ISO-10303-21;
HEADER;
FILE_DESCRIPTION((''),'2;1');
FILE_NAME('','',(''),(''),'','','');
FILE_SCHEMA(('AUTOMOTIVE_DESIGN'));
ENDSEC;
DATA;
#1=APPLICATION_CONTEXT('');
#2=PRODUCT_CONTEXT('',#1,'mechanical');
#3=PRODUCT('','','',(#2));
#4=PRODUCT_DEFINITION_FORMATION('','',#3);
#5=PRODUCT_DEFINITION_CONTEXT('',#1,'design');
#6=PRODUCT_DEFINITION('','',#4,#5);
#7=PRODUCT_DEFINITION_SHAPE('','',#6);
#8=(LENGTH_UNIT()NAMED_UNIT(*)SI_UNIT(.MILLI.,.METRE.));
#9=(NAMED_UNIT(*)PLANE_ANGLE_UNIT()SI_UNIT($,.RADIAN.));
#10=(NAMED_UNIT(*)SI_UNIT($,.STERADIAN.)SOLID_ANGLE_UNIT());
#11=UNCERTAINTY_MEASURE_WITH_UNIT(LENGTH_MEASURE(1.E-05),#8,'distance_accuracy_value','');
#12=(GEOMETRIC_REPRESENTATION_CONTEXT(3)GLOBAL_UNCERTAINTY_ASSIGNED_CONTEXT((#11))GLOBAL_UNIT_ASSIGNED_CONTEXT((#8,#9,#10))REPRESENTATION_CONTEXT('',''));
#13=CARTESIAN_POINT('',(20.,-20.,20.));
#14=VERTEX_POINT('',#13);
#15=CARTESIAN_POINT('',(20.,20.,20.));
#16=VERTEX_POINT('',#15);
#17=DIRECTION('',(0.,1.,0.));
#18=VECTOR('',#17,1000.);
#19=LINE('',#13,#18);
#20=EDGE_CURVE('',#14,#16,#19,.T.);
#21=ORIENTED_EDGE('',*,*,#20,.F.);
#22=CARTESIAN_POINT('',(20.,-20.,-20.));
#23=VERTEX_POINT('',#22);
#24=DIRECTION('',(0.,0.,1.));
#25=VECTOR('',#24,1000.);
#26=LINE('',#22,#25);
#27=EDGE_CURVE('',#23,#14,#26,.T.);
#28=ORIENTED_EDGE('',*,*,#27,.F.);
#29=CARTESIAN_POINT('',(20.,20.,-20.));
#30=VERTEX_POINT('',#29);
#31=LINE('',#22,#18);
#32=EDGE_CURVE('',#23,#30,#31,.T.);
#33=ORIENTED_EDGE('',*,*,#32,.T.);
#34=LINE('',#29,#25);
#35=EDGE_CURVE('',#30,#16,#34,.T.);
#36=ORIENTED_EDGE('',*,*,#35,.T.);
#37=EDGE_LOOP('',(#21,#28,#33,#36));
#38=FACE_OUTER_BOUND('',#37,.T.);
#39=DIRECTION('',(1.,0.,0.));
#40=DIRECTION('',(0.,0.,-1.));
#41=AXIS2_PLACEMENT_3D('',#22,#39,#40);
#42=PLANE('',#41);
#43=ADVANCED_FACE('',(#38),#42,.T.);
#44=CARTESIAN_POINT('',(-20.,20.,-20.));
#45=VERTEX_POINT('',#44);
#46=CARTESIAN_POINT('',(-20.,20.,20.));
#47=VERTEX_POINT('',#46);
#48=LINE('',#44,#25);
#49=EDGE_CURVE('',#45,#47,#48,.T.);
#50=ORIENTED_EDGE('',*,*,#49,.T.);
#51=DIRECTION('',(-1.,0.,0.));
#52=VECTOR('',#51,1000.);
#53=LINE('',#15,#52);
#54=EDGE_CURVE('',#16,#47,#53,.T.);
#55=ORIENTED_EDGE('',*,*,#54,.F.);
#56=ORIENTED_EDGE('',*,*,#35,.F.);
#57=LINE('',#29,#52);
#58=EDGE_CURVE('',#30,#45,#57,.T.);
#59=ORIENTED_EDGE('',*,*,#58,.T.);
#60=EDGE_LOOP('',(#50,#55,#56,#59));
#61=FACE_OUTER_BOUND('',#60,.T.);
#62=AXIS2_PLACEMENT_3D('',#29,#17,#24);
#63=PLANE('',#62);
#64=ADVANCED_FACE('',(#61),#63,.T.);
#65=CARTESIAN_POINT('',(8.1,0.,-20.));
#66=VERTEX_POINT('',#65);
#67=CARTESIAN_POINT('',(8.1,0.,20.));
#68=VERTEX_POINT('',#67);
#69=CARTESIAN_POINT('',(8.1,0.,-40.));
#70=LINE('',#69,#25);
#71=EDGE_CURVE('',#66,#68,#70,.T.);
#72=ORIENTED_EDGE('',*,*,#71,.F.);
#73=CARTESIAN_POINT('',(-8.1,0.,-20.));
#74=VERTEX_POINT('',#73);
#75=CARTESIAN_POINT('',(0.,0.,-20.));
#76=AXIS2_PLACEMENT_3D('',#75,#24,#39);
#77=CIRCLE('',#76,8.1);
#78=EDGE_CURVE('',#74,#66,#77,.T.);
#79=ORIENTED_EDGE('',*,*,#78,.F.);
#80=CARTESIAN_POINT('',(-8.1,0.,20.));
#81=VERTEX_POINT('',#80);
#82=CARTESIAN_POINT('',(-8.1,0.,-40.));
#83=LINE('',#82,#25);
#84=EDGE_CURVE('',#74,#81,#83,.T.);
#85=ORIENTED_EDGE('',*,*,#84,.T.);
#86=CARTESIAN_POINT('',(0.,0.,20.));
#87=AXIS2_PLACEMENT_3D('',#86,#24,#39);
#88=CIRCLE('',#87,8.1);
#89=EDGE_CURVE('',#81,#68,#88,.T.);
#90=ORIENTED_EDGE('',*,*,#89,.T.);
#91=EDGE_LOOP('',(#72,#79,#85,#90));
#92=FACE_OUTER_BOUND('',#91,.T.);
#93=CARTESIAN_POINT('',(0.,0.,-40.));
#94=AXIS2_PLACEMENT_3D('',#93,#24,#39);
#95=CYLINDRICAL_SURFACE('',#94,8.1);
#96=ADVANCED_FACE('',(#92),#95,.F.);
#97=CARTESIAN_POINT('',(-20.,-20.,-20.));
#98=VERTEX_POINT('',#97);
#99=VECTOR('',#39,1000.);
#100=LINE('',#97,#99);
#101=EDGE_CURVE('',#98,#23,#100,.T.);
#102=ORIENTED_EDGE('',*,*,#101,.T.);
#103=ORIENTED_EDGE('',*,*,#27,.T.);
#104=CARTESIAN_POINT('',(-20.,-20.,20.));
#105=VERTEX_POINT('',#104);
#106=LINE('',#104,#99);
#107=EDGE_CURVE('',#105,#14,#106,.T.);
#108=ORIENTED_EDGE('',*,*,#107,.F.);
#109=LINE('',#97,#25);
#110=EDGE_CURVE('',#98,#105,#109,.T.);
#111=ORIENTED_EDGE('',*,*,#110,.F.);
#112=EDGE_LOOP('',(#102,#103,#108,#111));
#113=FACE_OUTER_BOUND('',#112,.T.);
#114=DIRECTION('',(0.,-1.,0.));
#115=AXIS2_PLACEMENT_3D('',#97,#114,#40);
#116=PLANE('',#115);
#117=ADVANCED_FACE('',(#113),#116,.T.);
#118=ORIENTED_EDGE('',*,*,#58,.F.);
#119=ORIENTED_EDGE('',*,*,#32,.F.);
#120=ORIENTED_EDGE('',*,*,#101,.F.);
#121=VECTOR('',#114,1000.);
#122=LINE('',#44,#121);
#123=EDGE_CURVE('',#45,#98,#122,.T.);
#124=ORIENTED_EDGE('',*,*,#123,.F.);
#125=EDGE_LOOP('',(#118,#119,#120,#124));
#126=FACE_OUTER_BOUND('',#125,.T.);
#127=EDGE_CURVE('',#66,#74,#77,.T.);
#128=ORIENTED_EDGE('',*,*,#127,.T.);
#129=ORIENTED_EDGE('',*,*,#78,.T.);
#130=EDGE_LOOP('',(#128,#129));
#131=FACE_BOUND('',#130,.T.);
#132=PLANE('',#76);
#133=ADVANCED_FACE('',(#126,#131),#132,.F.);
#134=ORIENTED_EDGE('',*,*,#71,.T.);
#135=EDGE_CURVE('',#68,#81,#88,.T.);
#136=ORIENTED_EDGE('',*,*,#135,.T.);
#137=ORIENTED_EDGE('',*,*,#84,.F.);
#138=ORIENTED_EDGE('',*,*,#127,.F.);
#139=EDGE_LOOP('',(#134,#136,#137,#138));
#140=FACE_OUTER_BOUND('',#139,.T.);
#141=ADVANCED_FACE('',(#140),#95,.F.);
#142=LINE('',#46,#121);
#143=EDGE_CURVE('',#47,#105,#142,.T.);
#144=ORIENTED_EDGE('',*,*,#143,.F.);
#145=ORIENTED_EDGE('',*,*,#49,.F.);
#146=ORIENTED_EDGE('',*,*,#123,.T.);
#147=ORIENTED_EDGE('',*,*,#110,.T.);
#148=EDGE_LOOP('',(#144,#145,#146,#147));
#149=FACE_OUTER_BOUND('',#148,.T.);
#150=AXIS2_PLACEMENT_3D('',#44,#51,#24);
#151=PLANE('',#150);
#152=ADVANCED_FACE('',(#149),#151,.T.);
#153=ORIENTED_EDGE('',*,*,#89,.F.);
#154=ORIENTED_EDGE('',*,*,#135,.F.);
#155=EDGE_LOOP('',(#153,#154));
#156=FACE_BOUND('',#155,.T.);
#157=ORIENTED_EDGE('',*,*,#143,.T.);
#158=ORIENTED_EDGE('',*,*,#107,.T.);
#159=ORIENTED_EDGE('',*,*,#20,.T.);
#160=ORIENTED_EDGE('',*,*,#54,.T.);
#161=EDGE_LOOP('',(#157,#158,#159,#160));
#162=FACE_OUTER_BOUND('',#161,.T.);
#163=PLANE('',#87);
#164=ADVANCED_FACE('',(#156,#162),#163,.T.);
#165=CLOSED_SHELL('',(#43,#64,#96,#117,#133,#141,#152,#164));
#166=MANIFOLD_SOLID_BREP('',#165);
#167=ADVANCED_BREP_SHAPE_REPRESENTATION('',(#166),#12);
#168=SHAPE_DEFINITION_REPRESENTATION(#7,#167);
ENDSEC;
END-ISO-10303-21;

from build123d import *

# Parameters (mm, degrees)
SKETCH_1_W          = 40
SKETCH_1_H          = 40
EXTRUDE_1_DEPTH     = 20
SKETCH_2_R          = 8.1
CUT_EXTRUDE_1_DEPTH = 40


with BuildPart() as part:
    # 草图1 → 凸台-拉伸1 (new, symmetric)
    with BuildSketch(Plane.XY):
        Rectangle(SKETCH_1_W, SKETCH_1_H)
    extrude(amount=EXTRUDE_1_DEPTH, both=True)

    # 草图2 → 切除-拉伸1 (cut, symmetric)
    with BuildSketch(Plane.XY):
        Circle(SKETCH_2_R)
    extrude(amount=CUT_EXTRUDE_1_DEPTH, both=True, mode=Mode.SUBTRACT)


solid = part.part
